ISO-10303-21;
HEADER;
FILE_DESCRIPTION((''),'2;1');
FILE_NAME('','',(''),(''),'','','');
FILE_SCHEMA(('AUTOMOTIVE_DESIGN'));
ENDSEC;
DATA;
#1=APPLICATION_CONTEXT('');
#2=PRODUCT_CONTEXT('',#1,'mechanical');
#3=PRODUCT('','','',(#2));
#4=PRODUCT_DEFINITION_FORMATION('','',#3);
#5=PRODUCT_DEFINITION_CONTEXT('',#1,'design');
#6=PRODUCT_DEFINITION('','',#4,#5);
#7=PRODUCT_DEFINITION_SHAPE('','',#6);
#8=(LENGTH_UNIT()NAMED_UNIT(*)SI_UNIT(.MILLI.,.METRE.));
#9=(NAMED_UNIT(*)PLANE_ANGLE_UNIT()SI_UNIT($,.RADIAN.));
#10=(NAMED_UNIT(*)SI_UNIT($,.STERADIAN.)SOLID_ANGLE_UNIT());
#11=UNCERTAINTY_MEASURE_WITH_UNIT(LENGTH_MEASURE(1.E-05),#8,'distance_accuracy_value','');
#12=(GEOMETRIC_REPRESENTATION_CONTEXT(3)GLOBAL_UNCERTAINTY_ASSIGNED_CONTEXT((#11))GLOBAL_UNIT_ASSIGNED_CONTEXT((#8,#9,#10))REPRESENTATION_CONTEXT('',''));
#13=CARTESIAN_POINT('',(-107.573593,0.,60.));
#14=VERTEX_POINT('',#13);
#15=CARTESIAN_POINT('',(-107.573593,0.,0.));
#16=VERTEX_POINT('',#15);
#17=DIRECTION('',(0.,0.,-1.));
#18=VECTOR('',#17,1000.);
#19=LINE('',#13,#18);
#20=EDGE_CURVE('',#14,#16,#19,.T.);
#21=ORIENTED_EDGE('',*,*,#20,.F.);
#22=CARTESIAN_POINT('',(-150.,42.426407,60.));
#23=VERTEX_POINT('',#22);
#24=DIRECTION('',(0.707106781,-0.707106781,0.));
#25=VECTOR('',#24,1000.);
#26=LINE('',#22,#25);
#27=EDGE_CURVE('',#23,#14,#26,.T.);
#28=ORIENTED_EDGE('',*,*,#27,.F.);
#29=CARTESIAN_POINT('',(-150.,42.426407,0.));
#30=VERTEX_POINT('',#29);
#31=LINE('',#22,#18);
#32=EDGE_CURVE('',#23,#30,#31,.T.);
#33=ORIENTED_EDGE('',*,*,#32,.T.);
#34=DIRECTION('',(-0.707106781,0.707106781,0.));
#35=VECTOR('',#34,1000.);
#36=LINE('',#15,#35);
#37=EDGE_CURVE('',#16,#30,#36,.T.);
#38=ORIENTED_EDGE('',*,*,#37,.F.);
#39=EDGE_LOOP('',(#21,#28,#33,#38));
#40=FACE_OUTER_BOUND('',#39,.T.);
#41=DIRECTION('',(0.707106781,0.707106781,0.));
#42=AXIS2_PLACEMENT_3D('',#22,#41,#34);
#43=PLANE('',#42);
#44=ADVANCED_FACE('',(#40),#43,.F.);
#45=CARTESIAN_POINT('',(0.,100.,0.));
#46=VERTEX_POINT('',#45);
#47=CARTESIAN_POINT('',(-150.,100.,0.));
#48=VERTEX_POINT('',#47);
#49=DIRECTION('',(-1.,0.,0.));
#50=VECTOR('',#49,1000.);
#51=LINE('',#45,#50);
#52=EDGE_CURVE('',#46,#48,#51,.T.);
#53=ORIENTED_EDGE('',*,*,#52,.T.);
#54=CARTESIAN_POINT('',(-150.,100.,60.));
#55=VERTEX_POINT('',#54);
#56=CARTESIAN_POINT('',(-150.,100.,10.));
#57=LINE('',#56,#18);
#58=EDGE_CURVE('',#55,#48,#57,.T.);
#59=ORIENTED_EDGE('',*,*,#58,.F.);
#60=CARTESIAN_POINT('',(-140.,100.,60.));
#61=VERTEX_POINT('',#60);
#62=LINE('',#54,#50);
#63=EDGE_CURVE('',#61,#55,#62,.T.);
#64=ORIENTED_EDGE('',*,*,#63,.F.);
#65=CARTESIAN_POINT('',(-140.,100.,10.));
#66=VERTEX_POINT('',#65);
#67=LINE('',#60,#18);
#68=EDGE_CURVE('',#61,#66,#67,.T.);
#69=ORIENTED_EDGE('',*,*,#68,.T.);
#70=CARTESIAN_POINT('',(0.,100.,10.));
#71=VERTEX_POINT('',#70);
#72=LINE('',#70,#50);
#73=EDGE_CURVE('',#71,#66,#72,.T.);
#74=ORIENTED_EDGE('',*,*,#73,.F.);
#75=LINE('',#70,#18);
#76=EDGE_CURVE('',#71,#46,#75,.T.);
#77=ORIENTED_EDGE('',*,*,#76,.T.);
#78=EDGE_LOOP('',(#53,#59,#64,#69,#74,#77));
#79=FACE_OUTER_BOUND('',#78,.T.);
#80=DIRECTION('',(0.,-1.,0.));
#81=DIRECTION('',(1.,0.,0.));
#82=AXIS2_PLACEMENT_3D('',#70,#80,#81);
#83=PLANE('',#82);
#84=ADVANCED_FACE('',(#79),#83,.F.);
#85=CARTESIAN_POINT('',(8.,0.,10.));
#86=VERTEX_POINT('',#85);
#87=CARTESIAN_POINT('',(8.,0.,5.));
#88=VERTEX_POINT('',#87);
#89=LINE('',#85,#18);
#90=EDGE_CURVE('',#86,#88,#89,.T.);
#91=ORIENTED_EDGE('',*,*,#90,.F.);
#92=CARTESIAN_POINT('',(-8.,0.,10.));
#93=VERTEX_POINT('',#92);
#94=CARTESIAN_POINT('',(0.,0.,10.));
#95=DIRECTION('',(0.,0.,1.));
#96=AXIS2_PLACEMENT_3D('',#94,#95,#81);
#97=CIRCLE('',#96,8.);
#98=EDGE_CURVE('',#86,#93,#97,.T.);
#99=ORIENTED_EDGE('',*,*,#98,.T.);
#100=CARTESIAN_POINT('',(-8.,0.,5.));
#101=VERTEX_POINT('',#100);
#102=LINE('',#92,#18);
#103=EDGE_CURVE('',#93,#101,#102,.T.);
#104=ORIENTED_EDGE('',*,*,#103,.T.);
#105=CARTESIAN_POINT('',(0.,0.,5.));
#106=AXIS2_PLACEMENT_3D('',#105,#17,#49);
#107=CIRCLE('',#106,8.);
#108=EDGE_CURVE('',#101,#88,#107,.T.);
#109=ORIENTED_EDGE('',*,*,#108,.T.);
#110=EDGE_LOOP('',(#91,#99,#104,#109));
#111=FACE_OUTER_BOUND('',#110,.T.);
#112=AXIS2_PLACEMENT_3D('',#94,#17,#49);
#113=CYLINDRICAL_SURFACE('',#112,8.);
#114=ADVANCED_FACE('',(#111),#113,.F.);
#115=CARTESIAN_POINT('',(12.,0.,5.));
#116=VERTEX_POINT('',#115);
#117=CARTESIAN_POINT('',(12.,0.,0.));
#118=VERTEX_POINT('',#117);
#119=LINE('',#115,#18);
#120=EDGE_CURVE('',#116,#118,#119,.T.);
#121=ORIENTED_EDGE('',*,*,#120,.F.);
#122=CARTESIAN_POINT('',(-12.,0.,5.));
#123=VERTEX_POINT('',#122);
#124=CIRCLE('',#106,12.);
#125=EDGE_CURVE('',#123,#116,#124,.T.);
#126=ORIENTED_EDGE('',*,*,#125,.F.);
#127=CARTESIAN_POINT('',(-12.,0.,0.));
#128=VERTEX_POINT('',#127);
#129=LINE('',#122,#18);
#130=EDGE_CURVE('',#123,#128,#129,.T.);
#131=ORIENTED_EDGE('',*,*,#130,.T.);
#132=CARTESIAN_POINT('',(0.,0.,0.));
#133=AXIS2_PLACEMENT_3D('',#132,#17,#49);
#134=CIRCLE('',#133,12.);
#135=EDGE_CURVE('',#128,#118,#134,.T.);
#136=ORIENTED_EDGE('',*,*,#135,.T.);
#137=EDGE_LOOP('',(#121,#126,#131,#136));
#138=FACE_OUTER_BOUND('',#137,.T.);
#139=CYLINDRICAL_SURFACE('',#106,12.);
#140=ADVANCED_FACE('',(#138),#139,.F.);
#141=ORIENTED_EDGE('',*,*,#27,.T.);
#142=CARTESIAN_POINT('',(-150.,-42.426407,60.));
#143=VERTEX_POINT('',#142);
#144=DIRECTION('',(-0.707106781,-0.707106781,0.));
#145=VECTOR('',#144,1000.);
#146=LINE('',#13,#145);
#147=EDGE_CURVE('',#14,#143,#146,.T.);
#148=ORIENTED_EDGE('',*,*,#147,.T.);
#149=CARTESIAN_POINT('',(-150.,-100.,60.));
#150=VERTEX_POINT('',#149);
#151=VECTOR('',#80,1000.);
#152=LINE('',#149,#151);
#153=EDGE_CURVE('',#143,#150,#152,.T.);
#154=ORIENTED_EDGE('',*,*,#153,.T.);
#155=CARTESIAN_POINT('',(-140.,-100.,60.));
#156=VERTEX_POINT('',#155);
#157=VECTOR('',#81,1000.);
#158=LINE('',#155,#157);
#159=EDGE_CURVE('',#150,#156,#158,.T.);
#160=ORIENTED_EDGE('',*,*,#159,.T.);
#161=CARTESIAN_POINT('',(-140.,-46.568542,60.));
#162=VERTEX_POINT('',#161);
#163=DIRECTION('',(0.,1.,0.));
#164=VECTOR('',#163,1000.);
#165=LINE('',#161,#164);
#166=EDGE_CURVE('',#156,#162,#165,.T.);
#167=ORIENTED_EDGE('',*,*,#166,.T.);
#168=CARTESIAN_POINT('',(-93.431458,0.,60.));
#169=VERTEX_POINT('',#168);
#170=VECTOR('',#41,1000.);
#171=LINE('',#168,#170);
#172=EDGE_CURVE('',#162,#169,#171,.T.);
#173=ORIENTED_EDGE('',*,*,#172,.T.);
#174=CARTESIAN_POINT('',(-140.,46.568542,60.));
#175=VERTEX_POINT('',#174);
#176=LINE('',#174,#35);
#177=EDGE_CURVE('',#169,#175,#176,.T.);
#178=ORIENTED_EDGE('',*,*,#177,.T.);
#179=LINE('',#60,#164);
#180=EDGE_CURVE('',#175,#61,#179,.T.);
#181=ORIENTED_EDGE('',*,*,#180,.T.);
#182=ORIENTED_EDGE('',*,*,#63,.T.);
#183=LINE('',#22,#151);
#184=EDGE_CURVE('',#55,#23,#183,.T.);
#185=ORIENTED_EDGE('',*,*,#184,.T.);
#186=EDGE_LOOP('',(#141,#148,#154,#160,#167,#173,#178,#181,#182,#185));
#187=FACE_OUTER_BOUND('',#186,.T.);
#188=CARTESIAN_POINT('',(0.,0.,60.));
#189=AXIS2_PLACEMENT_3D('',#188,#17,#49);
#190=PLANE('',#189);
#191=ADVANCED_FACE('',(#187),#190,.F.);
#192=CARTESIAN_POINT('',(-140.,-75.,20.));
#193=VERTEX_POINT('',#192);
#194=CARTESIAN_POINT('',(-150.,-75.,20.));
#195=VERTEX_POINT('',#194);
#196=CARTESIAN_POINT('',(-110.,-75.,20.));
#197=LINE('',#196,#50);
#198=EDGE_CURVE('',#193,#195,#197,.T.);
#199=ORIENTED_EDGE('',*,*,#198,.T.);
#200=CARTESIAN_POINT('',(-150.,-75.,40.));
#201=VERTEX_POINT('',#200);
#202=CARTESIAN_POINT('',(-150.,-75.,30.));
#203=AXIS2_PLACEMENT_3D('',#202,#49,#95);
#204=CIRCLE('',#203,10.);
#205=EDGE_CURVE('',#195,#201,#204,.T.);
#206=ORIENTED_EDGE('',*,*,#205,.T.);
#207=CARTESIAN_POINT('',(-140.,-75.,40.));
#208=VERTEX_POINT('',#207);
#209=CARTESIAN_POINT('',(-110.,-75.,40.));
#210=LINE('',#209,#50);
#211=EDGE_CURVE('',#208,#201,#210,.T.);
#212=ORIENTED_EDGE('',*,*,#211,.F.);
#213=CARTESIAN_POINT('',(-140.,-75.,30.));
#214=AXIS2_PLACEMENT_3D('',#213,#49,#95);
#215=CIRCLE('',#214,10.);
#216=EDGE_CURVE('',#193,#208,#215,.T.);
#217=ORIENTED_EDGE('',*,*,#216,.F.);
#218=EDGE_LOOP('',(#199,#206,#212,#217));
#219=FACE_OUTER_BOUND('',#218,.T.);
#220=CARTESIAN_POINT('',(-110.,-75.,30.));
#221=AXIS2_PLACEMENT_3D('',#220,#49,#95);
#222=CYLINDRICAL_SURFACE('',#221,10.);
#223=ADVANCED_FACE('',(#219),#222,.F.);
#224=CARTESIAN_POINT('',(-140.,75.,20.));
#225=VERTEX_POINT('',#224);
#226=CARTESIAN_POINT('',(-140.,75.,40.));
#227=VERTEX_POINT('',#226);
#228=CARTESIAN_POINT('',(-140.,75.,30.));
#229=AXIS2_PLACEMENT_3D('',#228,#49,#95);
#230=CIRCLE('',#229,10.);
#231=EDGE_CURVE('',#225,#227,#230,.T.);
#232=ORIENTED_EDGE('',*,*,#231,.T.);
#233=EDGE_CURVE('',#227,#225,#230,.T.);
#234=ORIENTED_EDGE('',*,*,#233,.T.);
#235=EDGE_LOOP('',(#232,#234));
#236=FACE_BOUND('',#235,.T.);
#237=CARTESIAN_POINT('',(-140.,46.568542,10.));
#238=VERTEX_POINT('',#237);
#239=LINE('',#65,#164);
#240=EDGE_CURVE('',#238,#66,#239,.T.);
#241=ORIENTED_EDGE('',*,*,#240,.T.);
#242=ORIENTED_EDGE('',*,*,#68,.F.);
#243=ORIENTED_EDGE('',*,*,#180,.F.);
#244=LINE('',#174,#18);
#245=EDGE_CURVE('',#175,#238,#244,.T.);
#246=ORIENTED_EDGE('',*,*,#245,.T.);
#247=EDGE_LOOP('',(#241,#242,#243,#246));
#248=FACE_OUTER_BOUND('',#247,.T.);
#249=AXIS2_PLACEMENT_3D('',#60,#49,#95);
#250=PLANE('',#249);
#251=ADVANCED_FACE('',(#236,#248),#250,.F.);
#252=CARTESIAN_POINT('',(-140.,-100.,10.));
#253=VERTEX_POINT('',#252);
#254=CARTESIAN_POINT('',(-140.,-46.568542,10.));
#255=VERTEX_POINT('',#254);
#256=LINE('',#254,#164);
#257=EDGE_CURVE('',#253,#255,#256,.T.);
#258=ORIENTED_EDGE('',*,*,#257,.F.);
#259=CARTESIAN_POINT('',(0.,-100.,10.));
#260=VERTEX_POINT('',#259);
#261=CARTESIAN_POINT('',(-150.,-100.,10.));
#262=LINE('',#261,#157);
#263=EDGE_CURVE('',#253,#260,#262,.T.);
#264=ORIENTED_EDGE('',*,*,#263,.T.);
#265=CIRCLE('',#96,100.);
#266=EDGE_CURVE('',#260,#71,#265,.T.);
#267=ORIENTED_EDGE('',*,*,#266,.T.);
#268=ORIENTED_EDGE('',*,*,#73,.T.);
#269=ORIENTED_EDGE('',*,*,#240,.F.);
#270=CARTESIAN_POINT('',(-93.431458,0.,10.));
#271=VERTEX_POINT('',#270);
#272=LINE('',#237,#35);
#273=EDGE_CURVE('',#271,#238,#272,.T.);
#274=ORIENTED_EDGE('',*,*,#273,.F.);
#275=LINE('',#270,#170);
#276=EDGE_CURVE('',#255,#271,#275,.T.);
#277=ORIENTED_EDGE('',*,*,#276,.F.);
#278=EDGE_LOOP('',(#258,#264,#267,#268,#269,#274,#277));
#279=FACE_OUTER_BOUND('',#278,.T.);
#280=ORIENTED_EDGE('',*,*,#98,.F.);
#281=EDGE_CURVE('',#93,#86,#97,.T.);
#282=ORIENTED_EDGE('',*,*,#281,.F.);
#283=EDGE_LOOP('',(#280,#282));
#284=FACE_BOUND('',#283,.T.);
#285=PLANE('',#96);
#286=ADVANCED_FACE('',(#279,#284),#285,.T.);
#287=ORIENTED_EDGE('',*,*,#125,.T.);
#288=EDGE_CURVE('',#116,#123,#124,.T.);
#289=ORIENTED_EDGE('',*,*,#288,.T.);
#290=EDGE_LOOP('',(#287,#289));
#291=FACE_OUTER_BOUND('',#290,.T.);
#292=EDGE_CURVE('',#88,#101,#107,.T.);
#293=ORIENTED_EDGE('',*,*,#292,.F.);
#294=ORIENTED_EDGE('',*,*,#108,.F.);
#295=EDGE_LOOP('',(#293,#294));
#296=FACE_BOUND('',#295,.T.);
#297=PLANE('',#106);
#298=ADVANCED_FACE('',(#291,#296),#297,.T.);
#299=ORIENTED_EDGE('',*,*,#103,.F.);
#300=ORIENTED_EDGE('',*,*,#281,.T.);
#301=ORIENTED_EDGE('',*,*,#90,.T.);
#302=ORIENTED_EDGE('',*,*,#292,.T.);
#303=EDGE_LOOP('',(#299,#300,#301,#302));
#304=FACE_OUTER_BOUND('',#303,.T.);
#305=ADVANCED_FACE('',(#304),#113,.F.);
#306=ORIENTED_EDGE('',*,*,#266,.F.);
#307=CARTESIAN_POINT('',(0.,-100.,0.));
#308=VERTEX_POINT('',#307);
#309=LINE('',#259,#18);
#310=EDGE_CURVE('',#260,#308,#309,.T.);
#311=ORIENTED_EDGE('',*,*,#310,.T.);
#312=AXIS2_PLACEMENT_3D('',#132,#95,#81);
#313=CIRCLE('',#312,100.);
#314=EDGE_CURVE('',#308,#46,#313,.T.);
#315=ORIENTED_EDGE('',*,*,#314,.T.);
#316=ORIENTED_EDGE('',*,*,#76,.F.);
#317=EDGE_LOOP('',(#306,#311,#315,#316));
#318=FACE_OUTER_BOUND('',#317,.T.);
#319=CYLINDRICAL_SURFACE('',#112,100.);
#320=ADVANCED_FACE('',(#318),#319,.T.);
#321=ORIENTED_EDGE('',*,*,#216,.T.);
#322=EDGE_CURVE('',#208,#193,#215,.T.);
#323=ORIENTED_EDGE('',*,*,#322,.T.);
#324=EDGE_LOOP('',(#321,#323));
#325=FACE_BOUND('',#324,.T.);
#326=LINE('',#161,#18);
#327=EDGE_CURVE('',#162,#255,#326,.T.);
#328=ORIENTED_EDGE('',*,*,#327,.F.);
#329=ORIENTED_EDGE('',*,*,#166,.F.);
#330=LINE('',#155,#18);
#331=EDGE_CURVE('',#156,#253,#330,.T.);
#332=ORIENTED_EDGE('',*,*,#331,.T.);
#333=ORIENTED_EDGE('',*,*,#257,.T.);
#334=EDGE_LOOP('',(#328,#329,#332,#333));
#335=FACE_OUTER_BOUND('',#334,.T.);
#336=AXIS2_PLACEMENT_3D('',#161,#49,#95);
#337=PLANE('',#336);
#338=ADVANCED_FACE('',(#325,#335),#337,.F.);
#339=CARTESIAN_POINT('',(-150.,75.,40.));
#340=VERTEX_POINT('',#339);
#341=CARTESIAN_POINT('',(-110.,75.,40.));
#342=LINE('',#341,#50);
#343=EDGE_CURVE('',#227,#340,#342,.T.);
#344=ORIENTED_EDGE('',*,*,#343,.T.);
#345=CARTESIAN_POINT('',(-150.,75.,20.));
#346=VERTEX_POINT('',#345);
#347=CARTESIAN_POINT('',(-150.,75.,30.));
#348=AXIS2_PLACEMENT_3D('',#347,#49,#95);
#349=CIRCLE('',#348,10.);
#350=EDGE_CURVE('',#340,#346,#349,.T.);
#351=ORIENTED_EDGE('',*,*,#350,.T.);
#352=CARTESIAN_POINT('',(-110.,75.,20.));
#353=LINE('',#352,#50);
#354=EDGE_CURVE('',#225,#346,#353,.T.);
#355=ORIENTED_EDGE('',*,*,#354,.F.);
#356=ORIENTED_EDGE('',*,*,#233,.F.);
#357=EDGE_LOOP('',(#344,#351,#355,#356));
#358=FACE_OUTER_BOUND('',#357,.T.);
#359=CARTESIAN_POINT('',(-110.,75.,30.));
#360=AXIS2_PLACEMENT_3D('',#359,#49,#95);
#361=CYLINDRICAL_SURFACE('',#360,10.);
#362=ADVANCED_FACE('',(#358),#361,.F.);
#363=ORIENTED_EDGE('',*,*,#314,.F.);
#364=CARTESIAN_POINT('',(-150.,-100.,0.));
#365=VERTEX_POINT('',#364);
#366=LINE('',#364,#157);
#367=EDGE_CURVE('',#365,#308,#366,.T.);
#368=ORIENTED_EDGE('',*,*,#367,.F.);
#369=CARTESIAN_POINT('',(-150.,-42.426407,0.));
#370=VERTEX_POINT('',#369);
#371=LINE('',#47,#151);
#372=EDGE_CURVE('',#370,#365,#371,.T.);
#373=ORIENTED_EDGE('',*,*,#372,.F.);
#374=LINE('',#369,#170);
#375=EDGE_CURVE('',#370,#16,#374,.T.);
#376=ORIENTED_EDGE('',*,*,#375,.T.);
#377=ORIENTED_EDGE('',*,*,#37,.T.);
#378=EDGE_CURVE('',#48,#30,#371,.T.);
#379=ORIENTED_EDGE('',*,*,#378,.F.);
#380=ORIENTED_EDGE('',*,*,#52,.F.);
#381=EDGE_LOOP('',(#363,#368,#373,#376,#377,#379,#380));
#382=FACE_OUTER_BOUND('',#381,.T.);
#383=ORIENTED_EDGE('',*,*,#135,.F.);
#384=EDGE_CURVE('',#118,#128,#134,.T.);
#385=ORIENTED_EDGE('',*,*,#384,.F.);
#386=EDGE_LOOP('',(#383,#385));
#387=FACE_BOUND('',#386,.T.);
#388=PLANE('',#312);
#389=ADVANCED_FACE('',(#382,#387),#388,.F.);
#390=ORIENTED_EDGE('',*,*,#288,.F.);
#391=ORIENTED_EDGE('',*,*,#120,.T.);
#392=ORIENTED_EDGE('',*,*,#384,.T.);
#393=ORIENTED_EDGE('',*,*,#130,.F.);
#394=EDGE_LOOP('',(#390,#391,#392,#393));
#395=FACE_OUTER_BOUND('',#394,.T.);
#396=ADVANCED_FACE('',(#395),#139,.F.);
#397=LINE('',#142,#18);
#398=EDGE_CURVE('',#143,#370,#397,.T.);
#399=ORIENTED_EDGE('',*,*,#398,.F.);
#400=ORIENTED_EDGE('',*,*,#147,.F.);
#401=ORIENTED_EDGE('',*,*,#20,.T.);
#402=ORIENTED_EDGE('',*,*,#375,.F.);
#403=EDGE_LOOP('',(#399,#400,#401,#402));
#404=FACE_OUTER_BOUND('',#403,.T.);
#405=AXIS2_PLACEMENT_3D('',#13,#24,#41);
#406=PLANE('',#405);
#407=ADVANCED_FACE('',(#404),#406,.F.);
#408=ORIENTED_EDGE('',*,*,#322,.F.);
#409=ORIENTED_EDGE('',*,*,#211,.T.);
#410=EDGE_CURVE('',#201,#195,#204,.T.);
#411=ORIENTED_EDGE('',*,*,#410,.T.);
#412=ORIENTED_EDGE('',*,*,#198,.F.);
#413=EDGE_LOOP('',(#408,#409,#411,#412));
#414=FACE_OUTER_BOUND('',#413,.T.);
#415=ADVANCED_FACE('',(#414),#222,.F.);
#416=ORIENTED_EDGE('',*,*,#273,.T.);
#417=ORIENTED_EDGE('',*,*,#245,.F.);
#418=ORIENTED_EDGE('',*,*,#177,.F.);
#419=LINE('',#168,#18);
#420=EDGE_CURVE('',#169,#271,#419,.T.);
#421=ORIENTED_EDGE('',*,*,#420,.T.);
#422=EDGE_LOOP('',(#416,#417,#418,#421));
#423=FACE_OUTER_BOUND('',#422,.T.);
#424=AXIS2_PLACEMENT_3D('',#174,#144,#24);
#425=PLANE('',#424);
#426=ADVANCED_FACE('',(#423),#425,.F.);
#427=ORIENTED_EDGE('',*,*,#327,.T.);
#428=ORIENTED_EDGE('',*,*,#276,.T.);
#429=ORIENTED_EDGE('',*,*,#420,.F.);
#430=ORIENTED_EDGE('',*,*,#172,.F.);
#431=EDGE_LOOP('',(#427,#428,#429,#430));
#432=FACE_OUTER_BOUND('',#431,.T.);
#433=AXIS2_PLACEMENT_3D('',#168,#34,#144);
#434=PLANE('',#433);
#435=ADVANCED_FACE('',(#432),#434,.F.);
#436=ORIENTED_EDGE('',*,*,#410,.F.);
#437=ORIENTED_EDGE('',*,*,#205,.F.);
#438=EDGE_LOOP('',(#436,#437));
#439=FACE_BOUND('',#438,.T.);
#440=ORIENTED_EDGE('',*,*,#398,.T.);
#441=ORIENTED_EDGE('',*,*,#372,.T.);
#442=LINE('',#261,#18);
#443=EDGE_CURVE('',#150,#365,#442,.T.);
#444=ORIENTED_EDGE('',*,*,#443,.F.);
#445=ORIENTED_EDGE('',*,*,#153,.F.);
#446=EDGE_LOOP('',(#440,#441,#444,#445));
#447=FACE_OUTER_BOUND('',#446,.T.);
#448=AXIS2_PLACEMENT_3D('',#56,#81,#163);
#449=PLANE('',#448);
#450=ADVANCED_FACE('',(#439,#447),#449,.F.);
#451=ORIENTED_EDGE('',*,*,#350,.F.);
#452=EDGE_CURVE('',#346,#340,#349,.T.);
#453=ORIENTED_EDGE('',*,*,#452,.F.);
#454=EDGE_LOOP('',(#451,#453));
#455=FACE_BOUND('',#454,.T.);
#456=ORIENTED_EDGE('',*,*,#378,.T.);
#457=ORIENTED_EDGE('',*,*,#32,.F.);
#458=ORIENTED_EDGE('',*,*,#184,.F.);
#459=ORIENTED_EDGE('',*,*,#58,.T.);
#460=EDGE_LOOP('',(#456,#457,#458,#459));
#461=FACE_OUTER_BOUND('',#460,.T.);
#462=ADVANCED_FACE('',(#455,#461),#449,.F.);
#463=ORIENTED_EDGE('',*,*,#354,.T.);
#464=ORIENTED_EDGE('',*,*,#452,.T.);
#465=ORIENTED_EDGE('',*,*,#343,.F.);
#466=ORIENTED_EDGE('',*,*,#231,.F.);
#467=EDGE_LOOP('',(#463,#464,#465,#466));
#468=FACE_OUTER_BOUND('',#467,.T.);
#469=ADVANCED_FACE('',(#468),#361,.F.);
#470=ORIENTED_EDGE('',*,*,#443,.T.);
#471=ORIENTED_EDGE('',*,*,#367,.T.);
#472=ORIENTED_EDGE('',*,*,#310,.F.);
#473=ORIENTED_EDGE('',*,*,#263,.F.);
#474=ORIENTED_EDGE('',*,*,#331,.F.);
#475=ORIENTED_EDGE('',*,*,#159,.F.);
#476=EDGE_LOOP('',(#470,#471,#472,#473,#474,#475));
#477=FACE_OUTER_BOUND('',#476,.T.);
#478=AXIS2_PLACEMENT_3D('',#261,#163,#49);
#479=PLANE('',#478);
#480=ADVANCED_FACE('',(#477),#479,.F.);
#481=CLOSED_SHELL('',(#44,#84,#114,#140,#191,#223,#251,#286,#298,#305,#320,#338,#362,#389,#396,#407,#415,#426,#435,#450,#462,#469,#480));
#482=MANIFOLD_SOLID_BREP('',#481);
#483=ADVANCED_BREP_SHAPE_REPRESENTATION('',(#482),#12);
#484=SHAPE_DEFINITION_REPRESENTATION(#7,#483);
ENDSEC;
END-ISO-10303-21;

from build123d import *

# Parameters (mm, degrees)
SKETCH_1_R          = 8
EXTRUDE_1_DEPTH     = 10
EXTRUDE_2_DEPTH     = 50
CUT_EXTRUDE_1_DEPTH = 188.082869339
SKETCH_4_R          = 10
CUT_EXTRUDE_2_DEPTH = 40
SKETCH_6_R          = 12
CUT_EXTRUDE_4_DEPTH = 5


with BuildPart() as part:
    # 草图1 → 凸台-拉伸1 (new body)
    with BuildSketch(Plane.XY):
        with BuildLine():
            Line((0, 100), (-150, 100))
            Line((-150, 100), (-150, -100))
            Line((-150, -100), (0, -100))
            ThreePointArc((0, -100), (100, 0), (0, 100))
        make_face()
        Circle(SKETCH_1_R, mode=Mode.SUBTRACT)
    extrude(amount=EXTRUDE_1_DEPTH)

    # 草图2 → 凸台-拉伸2 (add)
    with BuildSketch(Plane.XY.offset(10)):
        Polygon((-150, 42.426406871), (-150, 100), (-140, 100), (-140, 46.568542495), (-93.431457505, 0), (-140, -46.568542495), (-140, -100), (-150, -100), (-150, -42.426406871), (-107.573593129, 0), align=None)
    extrude(amount=EXTRUDE_2_DEPTH)

    # 草图3 → 切除-拉伸1 (cut, through all)
    with BuildSketch(Plane.XY.offset(10)):
        Polygon((-150, -42.426406871), (-107.573593129, 0), (-150, 42.426406871), align=None)
    extrude(amount=-CUT_EXTRUDE_1_DEPTH, mode=Mode.SUBTRACT)

    # 草图4 → 切除-拉伸2 (cut)
    with BuildSketch(Plane.ZY.offset(150)):
        with Locations((30, -75)):
            Circle(SKETCH_4_R)
        with Locations((30, 75)):
            Circle(SKETCH_4_R)
    extrude(amount=-CUT_EXTRUDE_2_DEPTH, mode=Mode.SUBTRACT)

    # 草图6 → 切除-拉伸4 (cut)
    with BuildSketch(Plane(origin=(0, 0, 0), x_dir=(-1, 0, 0), z_dir=(0, 0, -1))):
        Circle(SKETCH_6_R)
    extrude(amount=-CUT_EXTRUDE_4_DEPTH, mode=Mode.SUBTRACT)


solid = part.part
